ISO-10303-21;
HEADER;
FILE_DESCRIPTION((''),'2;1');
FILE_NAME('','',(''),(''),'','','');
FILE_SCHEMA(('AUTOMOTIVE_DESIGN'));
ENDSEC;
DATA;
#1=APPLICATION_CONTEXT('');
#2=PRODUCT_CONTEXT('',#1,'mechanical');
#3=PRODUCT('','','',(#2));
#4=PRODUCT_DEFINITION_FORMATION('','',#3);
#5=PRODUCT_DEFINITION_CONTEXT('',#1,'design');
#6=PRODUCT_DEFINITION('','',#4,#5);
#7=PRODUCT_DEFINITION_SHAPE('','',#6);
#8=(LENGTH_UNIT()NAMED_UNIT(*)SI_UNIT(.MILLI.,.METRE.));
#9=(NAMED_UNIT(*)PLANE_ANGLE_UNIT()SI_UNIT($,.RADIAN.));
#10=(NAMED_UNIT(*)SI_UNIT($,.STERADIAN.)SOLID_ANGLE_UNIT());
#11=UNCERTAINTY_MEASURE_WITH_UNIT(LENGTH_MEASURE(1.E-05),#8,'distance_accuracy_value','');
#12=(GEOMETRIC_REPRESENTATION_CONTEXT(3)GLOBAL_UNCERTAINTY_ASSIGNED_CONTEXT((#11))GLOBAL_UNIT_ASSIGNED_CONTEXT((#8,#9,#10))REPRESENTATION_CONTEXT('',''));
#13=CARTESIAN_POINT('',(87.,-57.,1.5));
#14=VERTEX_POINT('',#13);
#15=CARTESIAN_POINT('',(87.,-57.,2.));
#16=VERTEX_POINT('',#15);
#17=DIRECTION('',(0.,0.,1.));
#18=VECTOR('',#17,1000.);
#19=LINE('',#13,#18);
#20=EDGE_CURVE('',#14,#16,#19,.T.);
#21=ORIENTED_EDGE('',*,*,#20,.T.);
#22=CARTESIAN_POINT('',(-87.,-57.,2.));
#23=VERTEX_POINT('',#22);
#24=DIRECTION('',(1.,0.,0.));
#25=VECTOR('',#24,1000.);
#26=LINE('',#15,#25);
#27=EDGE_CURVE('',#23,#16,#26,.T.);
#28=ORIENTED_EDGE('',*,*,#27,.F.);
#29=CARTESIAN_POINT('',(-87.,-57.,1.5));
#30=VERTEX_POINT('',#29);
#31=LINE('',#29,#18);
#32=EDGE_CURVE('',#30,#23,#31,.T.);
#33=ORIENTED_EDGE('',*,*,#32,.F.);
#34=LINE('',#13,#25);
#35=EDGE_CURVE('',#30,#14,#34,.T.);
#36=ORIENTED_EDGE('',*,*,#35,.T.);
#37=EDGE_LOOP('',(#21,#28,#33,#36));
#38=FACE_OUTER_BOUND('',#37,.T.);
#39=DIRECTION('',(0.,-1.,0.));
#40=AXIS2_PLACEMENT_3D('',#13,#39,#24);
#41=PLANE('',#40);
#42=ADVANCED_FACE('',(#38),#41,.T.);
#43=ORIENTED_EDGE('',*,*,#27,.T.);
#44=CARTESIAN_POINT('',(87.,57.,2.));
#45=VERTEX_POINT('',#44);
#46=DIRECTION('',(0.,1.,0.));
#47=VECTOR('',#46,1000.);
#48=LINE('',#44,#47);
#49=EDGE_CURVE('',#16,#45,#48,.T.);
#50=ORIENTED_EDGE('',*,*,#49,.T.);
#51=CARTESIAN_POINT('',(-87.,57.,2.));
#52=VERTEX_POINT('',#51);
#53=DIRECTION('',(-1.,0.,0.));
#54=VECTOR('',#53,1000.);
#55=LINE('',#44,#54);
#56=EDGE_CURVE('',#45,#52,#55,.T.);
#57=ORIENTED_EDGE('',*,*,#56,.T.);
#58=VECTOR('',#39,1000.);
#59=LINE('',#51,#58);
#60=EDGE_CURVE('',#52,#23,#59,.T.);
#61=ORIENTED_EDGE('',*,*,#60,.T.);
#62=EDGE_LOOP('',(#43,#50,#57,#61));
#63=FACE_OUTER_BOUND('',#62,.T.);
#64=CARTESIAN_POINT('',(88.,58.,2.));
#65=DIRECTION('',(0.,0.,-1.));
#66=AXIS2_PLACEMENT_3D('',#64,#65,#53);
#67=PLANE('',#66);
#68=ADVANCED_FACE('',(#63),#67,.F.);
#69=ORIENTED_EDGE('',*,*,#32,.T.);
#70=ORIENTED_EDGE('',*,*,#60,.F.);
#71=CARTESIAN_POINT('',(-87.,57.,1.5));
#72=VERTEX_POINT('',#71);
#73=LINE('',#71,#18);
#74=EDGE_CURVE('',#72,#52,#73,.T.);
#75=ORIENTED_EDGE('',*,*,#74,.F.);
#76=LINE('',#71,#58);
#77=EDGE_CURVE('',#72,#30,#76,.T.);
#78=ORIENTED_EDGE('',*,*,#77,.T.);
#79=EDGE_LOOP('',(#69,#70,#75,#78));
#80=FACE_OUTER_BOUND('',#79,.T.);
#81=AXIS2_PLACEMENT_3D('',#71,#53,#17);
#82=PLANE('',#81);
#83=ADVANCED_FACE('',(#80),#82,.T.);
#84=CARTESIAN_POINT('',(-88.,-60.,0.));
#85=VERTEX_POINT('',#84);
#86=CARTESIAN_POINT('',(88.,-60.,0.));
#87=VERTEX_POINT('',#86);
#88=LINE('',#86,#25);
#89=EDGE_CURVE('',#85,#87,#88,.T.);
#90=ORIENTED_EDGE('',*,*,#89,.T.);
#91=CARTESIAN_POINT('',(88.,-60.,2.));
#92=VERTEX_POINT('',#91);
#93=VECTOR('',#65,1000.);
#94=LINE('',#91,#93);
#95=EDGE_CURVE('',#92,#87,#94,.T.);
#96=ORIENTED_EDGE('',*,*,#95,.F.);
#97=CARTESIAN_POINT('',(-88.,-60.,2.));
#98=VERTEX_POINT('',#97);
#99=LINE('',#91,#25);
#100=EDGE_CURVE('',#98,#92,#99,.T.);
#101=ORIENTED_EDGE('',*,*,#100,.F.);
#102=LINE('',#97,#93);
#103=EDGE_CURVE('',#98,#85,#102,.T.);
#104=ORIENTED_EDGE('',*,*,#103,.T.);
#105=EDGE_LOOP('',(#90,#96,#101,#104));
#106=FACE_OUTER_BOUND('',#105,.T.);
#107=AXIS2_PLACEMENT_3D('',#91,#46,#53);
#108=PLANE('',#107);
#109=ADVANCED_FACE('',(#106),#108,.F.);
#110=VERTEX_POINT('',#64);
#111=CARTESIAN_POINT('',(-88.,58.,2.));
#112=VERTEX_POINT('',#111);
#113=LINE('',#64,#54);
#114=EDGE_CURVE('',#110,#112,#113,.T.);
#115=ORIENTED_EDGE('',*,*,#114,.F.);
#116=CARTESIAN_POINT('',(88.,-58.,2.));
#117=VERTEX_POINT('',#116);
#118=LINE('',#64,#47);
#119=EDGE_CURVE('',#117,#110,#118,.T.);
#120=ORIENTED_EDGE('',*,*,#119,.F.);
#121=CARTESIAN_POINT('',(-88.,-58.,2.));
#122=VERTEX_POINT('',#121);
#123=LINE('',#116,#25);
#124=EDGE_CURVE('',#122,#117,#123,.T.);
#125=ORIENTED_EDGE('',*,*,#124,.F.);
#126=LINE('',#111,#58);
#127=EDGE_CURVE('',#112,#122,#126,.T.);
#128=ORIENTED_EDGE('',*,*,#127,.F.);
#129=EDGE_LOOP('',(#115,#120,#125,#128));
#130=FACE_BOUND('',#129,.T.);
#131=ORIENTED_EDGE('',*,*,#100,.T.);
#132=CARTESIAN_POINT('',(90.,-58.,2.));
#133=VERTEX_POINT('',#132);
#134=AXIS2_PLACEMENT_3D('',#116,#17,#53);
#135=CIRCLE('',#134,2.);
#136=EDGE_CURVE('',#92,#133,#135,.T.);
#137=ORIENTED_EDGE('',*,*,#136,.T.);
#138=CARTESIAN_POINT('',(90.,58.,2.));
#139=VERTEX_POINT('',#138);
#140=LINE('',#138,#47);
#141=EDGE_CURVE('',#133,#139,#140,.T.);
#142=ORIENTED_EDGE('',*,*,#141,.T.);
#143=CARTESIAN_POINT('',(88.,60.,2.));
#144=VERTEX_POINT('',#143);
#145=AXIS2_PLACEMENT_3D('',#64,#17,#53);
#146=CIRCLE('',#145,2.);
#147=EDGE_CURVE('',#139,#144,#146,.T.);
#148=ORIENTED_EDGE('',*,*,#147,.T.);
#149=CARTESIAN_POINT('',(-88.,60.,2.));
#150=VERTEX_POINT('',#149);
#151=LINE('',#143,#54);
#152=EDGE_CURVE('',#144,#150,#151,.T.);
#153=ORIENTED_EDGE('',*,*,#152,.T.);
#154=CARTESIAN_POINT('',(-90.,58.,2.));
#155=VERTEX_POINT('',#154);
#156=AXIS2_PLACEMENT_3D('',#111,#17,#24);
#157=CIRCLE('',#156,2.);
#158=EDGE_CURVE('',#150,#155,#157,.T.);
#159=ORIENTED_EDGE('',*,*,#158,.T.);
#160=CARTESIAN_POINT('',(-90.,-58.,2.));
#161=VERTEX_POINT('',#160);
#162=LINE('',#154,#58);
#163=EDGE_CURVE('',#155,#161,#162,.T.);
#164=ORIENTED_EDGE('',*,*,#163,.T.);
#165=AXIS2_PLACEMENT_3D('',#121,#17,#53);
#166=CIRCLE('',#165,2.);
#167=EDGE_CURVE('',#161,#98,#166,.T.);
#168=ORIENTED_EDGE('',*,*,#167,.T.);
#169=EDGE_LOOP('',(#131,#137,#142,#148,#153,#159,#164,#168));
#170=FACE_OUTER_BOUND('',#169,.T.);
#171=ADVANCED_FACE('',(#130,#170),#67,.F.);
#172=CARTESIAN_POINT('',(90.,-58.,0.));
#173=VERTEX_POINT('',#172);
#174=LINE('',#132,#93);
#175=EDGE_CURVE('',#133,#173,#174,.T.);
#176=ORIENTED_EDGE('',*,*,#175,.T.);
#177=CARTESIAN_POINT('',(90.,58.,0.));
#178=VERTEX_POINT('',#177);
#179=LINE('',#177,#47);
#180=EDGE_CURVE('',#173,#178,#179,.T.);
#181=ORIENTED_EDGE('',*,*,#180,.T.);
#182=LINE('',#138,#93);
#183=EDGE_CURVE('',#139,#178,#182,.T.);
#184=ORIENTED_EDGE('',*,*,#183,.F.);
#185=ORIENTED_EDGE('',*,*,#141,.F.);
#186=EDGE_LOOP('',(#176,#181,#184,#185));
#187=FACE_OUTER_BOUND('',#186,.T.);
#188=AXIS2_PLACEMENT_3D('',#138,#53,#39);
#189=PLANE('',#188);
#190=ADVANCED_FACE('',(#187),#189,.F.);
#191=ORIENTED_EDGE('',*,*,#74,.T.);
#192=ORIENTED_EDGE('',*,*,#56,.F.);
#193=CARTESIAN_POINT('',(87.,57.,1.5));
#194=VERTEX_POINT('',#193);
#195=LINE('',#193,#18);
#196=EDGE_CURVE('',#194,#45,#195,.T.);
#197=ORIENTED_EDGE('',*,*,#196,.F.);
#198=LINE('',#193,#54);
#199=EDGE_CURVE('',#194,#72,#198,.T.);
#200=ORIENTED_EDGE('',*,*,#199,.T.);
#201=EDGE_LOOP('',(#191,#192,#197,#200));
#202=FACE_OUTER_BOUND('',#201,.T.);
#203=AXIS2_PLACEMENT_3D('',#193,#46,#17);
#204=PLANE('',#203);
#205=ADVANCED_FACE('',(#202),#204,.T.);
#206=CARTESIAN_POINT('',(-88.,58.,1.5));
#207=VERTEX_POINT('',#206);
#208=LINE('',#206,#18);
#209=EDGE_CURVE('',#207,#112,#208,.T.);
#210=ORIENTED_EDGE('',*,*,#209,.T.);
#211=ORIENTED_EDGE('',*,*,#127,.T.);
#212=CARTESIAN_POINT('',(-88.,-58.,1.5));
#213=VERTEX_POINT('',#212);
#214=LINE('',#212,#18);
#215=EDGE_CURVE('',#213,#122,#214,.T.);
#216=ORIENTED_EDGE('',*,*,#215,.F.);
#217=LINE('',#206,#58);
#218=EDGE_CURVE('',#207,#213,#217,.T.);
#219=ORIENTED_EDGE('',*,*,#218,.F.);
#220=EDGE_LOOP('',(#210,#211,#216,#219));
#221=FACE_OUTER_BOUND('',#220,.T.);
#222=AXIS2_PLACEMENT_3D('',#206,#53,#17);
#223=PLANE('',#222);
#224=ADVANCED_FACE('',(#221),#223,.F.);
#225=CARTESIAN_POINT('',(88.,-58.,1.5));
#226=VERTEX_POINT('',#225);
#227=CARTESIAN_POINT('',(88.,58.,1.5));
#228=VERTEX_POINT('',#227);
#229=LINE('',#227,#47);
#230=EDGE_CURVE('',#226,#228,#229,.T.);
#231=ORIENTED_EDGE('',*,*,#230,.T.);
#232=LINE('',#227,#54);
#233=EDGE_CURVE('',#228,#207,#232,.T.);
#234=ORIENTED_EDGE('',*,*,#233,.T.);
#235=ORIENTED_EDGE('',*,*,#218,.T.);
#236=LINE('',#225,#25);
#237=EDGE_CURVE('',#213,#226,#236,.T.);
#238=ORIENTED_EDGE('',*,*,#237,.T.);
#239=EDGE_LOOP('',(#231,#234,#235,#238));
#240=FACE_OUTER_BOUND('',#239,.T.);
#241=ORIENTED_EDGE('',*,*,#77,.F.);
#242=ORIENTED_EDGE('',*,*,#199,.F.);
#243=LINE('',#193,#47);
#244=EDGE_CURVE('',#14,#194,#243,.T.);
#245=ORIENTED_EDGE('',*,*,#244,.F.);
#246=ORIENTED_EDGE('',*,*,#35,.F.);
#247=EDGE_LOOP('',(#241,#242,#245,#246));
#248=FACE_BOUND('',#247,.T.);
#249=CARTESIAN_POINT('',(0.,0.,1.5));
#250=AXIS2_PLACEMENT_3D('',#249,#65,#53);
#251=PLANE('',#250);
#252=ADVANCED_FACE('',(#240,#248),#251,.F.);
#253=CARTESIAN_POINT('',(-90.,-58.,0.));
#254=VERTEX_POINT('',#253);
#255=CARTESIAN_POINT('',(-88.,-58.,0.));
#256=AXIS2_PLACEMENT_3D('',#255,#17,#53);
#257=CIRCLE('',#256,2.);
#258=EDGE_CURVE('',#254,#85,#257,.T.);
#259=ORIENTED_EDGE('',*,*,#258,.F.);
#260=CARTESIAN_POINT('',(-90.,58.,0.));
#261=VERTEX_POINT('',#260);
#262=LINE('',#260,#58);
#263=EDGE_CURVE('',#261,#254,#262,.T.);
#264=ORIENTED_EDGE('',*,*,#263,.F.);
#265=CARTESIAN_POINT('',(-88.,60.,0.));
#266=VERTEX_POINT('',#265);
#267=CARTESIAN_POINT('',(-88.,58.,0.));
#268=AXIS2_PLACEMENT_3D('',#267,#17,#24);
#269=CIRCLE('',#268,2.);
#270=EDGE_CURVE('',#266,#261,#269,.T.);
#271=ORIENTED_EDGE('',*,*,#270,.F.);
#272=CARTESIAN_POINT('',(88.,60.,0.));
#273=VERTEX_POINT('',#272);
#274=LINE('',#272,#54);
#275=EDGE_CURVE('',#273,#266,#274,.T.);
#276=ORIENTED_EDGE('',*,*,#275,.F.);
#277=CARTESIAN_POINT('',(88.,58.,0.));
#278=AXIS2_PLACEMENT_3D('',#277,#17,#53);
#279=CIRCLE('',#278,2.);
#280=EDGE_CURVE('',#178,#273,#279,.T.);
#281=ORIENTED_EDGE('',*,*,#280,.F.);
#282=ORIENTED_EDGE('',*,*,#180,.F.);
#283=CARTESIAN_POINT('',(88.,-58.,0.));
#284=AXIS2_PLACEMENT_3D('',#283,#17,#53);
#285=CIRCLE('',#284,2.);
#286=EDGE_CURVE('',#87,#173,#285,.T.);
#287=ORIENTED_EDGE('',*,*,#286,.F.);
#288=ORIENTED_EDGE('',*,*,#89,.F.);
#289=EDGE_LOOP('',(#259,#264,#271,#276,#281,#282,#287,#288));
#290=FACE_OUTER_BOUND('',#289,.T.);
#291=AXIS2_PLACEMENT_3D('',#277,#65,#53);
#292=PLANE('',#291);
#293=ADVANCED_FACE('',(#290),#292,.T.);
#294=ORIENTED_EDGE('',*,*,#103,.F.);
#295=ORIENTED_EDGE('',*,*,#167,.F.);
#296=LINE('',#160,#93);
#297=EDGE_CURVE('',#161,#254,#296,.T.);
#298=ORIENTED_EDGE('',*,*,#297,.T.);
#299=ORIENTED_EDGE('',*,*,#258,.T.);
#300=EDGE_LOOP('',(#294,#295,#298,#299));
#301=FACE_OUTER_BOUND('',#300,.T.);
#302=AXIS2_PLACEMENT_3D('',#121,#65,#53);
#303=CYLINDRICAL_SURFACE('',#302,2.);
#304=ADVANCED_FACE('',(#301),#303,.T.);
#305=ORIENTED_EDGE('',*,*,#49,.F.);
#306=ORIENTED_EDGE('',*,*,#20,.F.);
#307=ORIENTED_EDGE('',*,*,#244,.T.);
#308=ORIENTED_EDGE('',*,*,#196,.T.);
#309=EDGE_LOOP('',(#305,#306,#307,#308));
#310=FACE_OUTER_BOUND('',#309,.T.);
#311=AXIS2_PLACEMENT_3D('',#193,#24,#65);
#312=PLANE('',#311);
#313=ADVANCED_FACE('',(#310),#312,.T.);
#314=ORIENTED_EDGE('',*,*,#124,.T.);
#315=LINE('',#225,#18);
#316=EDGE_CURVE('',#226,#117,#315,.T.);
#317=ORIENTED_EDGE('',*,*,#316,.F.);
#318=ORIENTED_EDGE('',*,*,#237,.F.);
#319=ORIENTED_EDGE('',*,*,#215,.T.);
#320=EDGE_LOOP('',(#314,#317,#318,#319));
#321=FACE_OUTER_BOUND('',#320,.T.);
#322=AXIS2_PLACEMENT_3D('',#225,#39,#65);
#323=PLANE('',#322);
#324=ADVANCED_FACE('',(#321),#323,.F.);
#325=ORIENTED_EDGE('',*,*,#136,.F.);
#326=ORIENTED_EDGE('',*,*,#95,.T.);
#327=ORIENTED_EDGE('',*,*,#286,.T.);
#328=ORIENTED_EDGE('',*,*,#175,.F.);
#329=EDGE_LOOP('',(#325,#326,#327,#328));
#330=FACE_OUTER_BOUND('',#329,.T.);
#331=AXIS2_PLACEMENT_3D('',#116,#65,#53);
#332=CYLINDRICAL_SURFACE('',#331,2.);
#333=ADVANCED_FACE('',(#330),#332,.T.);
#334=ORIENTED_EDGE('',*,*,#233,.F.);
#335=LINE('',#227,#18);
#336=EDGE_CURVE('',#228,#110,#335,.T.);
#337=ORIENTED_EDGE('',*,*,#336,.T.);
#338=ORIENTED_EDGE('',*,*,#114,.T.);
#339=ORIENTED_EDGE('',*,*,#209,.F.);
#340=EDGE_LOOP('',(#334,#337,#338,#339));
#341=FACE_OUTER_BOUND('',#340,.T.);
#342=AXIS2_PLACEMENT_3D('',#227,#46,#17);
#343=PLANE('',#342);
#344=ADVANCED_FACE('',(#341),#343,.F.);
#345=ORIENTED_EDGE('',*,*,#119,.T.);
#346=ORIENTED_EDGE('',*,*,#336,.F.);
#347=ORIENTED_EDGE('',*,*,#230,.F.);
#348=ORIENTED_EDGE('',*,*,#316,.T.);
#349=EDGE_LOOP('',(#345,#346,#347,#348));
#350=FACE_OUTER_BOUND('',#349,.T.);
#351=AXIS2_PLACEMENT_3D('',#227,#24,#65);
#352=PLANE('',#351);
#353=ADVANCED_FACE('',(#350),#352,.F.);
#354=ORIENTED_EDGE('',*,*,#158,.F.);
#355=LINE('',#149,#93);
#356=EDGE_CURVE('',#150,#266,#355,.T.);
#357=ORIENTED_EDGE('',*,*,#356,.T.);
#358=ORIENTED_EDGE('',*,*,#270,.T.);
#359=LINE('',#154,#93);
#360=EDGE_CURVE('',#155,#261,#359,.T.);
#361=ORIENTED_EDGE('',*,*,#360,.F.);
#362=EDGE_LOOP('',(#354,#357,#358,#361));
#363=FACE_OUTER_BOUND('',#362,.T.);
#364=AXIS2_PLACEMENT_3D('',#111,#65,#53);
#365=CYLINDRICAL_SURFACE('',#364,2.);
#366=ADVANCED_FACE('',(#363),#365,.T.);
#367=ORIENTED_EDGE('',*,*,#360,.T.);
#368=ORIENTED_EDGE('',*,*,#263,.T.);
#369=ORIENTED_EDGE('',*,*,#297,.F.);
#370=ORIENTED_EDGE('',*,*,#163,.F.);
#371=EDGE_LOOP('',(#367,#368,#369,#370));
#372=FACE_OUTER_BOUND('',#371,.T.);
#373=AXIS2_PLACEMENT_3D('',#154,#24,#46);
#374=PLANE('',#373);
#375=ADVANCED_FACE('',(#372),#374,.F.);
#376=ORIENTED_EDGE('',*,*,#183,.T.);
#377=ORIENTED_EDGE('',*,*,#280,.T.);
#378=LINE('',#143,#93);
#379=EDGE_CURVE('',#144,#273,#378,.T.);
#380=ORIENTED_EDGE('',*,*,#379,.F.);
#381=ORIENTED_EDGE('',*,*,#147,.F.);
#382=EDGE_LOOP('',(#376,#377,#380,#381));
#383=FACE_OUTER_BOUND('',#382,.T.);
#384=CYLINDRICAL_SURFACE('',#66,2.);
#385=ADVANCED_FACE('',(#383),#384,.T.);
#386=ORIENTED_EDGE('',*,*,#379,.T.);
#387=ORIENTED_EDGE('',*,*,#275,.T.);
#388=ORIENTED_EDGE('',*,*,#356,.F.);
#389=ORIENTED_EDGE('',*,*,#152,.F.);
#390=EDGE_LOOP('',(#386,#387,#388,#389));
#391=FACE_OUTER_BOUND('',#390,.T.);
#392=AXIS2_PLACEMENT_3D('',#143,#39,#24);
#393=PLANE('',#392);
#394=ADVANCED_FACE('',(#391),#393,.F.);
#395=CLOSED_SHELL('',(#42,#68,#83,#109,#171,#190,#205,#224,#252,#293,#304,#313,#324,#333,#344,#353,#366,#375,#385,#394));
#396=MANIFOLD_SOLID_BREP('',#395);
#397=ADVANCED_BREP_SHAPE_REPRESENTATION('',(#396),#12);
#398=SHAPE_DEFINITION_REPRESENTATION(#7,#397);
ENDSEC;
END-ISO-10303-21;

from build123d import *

# Parameters (mm, degrees)
BOSS_EXTRUDE1_DEPTH = 2
SKETCH2_W           = 176
SKETCH2_H           = 116
SKETCH2_W_2         = 174
SKETCH2_H_2         = 114
CUT_EXTRUDE1_DEPTH  = 0.5


with BuildPart() as part:
    # Sketch1 → Boss-Extrude1 (new body)
    with BuildSketch(Plane.XY):
        with BuildLine():
            Line((88, 60), (-88, 60))
            ThreePointArc((-88, 60), (-89.414213562, 59.414213562), (-90, 58))
            Line((-90, 58), (-90, -58))
            ThreePointArc((-90, -58), (-89.414213562, -59.414213562), (-88, -60))
            Line((-88, -60), (88, -60))
            ThreePointArc((88, -60), (89.414213562, -59.414213562), (90, -58))
            Line((90, -58), (90, 58))
            ThreePointArc((90, 58), (89.414213562, 59.414213562), (88, 60))
        make_face()
    extrude(amount=BOSS_EXTRUDE1_DEPTH)

    # Sketch2 → Cut-Extrude1 (cut)
    with BuildSketch(Plane.XY.offset(2)):
        Rectangle(SKETCH2_W, SKETCH2_H)
        Rectangle(SKETCH2_W_2, SKETCH2_H_2, mode=Mode.SUBTRACT)
    extrude(amount=-CUT_EXTRUDE1_DEPTH, mode=Mode.SUBTRACT)


solid = part.part
